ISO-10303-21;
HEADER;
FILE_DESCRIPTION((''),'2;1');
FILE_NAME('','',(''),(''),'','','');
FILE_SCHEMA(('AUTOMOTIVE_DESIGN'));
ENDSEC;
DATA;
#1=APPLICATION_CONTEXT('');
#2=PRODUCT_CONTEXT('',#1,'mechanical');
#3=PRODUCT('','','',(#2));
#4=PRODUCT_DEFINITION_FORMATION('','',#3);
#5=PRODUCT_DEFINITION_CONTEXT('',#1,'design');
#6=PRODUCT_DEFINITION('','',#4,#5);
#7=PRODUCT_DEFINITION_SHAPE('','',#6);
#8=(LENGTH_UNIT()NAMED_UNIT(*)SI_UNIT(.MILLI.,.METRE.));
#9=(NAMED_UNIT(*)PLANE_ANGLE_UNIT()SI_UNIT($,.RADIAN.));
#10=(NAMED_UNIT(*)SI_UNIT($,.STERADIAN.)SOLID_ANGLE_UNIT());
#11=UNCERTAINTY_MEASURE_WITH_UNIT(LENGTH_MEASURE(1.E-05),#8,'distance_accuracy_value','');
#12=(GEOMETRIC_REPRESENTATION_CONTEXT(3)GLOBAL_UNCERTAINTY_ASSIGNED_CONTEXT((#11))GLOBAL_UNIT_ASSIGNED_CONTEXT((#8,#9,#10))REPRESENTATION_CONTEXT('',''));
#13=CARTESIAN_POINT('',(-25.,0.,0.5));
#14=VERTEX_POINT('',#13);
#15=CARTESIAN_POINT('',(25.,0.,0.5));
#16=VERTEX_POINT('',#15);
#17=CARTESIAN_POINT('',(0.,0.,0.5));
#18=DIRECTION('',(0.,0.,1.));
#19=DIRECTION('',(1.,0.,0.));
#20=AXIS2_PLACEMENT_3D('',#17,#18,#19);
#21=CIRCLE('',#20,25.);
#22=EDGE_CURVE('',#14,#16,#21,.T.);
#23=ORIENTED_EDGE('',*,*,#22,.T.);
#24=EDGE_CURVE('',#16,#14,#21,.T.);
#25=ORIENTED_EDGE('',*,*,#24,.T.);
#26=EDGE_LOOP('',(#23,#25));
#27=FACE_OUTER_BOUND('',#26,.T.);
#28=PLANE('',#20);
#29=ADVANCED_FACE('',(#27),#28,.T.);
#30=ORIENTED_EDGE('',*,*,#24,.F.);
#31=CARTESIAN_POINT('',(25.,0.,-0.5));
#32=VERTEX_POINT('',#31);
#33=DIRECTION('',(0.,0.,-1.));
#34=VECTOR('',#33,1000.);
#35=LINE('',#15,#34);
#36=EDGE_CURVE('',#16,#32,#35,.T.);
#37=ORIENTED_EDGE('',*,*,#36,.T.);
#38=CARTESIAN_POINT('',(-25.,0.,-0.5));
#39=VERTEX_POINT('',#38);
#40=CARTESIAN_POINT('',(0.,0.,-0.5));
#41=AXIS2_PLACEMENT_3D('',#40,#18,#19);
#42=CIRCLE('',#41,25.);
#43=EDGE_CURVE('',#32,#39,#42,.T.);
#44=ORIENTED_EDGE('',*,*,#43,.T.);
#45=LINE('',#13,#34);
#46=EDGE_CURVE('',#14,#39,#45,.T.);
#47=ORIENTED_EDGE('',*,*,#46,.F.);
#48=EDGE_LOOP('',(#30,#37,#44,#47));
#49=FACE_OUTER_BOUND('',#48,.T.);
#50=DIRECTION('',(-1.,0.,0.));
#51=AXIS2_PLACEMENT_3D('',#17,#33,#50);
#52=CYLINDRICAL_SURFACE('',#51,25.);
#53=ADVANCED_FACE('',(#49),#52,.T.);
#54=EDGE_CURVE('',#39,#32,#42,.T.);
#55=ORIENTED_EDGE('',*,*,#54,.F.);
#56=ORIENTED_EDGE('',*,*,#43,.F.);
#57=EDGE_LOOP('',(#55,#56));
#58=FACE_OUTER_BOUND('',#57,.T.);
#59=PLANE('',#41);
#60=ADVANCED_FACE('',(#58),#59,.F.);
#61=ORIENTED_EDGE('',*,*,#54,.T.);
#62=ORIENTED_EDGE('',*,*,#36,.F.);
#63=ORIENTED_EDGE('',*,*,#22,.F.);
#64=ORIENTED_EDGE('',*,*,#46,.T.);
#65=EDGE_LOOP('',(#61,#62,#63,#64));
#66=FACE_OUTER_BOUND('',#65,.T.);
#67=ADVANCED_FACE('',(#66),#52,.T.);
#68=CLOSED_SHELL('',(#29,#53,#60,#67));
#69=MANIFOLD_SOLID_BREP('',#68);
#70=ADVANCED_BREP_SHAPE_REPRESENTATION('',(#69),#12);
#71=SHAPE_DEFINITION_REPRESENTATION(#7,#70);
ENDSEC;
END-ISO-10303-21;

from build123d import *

# Parameters (mm, degrees)
SKETCH_1_R      = 25
EXTRUDE_1_DEPTH = 0.5


with BuildPart() as part:
    # 草图1 → 凸台-拉伸1 (new, symmetric)
    with BuildSketch(Plane.XY):
        Circle(SKETCH_1_R)
    extrude(amount=EXTRUDE_1_DEPTH, both=True)


solid = part.part
